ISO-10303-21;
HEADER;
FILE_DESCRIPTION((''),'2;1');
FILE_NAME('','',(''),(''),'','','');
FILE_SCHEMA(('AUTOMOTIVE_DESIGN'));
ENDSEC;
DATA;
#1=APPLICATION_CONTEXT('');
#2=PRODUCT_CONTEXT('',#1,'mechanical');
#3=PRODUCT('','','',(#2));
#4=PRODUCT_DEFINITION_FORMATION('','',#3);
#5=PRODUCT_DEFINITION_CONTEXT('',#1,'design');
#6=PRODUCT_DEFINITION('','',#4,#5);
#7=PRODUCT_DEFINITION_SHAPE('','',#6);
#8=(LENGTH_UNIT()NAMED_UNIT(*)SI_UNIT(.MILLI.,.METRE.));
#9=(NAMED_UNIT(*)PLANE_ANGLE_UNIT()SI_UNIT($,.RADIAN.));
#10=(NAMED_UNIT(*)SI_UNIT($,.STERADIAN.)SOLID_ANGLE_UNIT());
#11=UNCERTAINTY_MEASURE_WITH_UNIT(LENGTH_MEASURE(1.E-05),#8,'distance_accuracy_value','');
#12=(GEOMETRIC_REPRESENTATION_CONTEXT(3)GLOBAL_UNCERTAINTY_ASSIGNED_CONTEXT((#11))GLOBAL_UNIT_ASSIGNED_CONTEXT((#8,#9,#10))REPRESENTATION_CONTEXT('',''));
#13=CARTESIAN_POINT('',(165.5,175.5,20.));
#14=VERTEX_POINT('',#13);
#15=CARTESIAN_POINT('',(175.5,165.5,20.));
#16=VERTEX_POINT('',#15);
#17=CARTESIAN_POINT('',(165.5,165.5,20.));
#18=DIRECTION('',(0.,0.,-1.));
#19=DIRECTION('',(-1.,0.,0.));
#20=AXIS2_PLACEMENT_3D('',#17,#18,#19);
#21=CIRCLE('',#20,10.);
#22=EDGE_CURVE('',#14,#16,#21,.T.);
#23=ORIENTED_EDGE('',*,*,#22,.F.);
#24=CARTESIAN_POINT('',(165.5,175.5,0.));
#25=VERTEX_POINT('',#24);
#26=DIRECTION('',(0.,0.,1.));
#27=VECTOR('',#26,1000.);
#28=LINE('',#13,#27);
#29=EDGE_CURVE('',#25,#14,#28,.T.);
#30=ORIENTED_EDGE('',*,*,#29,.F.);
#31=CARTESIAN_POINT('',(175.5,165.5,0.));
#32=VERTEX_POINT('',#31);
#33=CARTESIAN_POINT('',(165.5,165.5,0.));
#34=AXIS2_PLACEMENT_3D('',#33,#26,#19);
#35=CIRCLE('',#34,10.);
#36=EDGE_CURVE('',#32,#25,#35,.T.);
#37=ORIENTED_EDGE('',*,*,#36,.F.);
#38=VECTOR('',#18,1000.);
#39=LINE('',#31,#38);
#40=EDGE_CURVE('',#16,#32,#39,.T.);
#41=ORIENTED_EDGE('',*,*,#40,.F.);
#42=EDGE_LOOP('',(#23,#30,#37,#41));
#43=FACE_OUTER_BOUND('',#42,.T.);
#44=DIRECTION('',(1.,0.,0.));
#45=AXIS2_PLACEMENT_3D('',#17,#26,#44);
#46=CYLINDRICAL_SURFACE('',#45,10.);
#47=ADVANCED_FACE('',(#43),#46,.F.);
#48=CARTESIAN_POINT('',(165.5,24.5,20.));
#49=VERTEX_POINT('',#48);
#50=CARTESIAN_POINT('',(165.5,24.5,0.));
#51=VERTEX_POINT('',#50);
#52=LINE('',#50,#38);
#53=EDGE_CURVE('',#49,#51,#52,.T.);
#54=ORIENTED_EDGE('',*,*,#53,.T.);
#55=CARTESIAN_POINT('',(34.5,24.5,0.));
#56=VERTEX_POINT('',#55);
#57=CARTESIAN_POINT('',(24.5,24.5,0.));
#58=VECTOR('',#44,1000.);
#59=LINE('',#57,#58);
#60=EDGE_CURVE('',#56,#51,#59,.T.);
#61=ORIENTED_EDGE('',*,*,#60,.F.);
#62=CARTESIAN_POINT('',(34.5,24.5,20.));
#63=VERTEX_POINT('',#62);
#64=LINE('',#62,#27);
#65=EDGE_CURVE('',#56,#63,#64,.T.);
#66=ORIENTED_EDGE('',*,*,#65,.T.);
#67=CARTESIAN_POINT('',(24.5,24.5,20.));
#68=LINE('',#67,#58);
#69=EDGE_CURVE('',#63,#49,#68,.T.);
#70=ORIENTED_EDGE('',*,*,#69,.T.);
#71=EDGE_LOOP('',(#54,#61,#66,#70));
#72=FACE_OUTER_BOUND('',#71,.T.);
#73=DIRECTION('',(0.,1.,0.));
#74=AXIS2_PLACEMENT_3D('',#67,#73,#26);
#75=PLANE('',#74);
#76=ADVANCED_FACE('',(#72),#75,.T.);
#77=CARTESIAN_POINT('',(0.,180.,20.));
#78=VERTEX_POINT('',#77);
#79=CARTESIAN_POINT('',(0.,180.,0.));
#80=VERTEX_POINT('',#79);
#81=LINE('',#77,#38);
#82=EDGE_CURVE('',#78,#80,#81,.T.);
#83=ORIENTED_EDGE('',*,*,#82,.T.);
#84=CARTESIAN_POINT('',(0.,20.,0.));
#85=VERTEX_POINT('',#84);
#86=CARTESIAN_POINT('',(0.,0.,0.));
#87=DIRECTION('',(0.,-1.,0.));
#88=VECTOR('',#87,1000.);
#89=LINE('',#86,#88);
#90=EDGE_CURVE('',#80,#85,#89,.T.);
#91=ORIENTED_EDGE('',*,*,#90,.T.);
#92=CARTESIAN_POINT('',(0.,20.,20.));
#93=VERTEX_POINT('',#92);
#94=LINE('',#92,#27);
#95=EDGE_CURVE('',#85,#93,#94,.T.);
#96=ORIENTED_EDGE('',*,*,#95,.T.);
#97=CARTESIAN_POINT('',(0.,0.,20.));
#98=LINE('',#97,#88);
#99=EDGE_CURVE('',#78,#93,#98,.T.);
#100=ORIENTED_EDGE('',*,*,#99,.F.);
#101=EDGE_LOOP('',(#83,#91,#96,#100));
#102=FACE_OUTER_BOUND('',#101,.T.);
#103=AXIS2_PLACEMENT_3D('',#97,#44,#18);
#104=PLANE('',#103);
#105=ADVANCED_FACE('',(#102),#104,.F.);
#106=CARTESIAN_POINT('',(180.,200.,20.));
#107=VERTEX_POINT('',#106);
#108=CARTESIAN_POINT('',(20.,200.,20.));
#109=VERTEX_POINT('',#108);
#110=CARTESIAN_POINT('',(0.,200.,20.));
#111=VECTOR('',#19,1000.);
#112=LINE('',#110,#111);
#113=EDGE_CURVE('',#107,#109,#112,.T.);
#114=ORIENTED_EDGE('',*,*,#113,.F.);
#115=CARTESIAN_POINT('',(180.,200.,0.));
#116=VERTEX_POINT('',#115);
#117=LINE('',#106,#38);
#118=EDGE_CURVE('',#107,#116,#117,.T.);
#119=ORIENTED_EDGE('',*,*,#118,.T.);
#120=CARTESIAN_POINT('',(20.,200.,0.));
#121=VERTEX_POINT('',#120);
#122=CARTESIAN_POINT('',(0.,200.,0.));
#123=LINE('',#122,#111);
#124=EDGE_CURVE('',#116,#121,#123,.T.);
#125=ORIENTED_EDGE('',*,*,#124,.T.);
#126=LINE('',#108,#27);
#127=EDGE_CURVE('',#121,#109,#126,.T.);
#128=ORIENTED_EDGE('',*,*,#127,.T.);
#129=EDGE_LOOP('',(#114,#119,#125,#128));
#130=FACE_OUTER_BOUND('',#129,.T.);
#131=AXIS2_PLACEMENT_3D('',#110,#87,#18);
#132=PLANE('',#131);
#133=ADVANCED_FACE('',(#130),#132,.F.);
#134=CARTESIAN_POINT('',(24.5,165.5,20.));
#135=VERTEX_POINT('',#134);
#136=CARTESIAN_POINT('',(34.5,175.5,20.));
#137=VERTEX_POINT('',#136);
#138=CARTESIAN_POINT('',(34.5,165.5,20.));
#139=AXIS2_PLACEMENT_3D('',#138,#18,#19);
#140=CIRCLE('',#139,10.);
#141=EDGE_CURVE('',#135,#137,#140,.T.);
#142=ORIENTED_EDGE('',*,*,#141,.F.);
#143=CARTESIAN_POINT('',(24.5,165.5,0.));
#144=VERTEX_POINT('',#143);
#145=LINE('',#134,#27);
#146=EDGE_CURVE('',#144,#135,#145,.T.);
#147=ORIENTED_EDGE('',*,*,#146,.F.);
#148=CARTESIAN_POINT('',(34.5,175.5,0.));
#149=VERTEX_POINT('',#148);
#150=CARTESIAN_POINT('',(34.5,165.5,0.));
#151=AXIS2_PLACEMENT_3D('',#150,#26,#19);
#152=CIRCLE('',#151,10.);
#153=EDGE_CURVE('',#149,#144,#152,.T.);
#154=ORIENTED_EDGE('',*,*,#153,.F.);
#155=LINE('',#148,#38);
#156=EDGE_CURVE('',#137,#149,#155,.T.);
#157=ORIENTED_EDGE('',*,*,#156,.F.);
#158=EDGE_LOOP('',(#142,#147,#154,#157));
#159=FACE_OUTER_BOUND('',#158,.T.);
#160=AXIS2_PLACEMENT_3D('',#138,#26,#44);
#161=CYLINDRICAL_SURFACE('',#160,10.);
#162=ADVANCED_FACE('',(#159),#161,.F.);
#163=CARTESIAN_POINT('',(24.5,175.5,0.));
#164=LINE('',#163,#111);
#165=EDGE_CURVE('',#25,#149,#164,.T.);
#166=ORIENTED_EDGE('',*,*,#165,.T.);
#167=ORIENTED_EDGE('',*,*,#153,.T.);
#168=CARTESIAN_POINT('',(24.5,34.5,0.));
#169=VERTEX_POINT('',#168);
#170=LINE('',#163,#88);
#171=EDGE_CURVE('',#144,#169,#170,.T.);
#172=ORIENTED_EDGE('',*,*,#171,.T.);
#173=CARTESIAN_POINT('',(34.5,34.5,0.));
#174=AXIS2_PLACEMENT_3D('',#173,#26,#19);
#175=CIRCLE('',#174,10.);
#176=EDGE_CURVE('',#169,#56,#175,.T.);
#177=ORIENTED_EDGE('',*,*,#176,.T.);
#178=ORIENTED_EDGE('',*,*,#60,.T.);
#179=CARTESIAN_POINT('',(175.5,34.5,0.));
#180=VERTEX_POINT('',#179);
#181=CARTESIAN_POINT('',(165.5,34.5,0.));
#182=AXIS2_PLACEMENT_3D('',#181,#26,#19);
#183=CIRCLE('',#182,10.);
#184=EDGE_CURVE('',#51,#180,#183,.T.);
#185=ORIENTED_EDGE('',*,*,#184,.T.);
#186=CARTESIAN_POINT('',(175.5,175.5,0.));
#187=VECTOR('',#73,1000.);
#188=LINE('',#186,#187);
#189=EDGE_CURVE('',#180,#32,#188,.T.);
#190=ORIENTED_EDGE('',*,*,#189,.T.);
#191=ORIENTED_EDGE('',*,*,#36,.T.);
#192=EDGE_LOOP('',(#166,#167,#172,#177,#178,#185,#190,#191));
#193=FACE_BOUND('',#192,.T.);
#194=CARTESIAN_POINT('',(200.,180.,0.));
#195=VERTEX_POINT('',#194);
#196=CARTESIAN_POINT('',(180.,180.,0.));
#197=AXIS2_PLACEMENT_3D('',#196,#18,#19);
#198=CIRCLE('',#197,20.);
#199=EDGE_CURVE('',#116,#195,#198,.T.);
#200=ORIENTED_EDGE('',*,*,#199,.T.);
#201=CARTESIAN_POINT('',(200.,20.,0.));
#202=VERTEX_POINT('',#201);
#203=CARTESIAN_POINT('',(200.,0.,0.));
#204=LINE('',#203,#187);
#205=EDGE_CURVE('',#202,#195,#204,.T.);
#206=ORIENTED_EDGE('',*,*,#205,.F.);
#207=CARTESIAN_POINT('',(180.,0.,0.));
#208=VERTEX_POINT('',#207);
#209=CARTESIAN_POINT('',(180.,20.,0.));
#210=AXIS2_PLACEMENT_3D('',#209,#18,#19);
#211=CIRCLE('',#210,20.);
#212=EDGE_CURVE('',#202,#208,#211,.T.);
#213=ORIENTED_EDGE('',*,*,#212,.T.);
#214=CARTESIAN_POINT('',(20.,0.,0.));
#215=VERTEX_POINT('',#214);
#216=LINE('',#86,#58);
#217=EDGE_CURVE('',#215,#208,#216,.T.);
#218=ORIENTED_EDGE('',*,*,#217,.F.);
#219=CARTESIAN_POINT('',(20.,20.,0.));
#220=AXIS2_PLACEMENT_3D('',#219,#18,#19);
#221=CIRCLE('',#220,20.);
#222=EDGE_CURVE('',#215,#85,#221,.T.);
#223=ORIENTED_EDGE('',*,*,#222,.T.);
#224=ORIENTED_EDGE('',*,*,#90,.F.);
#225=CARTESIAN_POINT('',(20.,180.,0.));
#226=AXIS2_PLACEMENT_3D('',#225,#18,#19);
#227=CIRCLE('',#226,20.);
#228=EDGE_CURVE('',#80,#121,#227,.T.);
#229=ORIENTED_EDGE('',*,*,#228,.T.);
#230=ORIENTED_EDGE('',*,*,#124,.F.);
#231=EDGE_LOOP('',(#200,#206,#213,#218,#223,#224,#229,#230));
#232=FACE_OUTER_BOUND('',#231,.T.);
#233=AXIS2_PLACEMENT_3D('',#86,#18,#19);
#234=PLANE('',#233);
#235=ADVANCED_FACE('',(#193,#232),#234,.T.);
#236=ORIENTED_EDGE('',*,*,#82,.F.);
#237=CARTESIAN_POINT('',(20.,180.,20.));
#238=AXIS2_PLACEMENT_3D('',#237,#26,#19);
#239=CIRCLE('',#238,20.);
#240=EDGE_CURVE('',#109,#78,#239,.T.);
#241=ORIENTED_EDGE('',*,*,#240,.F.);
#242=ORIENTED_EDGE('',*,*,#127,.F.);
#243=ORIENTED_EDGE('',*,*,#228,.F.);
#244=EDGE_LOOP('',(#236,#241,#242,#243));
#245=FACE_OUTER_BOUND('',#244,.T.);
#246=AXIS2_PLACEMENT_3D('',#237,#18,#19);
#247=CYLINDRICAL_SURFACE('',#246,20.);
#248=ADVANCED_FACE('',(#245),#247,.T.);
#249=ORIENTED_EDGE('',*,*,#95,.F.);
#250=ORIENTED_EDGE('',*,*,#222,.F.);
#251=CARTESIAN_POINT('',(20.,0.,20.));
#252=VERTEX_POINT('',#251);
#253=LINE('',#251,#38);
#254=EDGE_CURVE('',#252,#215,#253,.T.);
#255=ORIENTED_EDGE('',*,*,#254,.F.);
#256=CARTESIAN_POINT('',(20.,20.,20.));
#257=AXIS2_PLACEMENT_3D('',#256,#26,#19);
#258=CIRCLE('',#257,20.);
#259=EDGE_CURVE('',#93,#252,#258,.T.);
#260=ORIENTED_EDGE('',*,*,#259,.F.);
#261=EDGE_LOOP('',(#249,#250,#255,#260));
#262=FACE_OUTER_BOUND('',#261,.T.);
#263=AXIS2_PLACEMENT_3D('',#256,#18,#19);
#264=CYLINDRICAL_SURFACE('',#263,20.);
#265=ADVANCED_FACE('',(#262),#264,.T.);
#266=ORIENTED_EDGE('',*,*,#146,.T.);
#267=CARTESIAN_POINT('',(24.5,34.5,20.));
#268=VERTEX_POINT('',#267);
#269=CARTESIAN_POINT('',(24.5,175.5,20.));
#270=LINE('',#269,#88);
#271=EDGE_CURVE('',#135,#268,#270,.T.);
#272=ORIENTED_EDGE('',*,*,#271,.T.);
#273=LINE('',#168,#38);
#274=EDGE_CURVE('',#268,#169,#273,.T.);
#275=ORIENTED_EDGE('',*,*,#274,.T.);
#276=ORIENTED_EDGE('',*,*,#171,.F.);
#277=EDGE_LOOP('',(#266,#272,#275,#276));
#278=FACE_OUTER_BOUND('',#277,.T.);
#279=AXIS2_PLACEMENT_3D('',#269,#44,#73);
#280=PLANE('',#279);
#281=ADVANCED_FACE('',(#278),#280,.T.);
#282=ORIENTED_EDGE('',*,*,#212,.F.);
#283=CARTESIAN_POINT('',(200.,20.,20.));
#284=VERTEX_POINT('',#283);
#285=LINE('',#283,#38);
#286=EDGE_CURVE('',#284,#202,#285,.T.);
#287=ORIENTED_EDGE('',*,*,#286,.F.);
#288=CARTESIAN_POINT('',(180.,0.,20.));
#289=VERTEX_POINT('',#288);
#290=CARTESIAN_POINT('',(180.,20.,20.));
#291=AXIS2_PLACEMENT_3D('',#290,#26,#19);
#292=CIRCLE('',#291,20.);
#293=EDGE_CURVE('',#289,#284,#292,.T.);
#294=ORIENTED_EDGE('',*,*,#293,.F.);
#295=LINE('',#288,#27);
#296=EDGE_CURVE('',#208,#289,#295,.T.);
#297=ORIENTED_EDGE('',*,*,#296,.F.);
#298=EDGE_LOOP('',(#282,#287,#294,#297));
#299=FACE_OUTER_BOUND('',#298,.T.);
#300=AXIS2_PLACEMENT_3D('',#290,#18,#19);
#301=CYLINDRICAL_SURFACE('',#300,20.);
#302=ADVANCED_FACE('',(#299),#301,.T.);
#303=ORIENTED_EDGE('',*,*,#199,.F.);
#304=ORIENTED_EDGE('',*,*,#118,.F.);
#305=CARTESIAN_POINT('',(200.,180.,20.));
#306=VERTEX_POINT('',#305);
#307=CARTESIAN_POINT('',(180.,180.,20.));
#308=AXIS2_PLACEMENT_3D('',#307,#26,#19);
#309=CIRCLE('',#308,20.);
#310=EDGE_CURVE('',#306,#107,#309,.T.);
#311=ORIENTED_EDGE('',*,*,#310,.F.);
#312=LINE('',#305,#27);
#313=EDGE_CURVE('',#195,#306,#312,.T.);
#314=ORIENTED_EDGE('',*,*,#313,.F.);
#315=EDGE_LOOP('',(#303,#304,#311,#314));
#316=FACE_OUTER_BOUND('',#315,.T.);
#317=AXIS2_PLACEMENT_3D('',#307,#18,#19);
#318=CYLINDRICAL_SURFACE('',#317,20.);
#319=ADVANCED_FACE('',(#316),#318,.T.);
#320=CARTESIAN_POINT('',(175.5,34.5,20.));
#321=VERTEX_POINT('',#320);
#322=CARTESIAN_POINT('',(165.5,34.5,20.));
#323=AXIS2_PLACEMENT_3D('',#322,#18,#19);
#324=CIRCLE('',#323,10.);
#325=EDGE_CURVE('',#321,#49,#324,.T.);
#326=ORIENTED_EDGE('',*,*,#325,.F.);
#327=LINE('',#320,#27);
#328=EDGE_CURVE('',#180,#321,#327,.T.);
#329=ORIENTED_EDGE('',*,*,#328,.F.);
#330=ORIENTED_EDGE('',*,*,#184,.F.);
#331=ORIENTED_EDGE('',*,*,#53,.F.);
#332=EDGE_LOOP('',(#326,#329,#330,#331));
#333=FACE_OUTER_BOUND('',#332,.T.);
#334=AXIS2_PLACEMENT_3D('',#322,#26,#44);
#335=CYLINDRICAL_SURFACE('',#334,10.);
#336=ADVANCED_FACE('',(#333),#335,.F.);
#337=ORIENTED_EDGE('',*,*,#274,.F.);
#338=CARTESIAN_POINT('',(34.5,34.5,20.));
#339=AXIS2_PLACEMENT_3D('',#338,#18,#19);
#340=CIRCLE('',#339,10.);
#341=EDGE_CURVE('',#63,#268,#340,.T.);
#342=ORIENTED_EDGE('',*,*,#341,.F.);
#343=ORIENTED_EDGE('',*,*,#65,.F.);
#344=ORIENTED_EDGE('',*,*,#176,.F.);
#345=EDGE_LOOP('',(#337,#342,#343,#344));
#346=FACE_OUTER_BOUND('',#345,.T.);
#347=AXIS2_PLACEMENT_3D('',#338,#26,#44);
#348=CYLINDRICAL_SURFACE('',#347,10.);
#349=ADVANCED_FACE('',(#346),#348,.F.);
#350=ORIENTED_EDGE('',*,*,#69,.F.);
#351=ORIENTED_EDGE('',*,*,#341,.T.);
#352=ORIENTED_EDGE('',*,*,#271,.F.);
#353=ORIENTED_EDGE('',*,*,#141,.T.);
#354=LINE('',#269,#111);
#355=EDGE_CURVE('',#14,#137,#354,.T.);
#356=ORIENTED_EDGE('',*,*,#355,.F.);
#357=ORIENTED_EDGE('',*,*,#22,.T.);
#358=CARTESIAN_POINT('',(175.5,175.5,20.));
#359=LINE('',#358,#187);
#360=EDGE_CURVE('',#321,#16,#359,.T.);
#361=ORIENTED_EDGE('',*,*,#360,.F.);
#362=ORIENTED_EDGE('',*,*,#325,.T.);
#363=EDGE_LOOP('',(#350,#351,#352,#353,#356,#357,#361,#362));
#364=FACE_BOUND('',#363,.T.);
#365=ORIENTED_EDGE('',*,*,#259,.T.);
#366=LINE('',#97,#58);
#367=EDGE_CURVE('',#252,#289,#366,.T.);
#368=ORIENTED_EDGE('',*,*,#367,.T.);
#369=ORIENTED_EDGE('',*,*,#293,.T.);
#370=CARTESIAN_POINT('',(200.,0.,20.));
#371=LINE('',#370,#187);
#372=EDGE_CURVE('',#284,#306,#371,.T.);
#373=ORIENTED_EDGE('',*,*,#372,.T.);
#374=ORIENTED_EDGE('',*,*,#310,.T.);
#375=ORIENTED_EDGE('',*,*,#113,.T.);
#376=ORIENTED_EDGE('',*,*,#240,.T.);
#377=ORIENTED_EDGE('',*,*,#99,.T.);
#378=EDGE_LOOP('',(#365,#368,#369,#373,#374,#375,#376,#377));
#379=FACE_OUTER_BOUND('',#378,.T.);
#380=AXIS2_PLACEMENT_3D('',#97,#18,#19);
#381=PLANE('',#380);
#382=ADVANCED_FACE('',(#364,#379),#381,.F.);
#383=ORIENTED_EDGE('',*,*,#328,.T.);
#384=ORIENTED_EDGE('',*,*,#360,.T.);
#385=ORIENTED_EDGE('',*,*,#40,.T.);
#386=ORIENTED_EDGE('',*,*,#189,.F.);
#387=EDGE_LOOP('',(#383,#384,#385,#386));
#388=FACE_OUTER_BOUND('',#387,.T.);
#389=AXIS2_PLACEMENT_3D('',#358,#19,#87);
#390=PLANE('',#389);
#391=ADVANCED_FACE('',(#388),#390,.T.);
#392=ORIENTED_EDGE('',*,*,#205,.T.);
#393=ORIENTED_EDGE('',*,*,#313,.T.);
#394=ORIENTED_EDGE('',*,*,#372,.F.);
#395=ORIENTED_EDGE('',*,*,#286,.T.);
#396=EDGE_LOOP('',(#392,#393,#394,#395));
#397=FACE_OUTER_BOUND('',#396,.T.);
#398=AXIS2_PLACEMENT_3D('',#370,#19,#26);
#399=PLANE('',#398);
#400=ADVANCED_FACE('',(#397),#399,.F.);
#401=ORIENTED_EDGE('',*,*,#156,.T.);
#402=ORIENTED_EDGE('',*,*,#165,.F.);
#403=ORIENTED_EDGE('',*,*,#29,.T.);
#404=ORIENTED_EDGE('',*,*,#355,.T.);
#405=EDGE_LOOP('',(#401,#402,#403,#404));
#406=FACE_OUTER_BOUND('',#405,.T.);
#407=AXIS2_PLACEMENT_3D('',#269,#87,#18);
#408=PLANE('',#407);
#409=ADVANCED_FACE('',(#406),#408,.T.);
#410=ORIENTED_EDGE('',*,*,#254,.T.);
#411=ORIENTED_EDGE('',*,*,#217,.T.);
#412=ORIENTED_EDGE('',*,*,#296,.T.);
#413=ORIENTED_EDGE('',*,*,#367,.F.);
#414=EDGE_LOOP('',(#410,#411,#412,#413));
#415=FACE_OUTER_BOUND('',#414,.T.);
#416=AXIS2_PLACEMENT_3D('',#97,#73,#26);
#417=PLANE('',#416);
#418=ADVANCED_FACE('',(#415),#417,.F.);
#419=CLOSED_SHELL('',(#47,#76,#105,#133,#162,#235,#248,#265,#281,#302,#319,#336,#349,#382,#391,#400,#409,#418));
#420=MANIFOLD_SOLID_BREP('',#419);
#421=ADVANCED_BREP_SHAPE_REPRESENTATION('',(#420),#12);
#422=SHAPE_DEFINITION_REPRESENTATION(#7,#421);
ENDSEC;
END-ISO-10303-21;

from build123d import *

# Parameters (mm, degrees)
SKETCH1_W           = 200
SKETCH1_H           = 200
SKETCH1_W_2         = 151
SKETCH1_H_2         = 151
BOSS_EXTRUDE1_DEPTH = 20
FILLET1_R           = 20
FILLET2_R           = 10


with BuildPart() as part:
    # Sketch1 → Boss-Extrude1 (new body)
    with BuildSketch(Plane.XY):
        with Locations((100, 100)):
            Rectangle(SKETCH1_W, SKETCH1_H)
        with Locations((100, 100)):
            Rectangle(SKETCH1_W_2, SKETCH1_H_2, mode=Mode.SUBTRACT)
    extrude(amount=BOSS_EXTRUDE1_DEPTH)

    # Fillet1
    fillet1_edges = [part.edges().sort_by_distance(p)[0] for p in [
        (0, 200, 10),
        (200, 200, 10),
        (200, 0, 10),
        (0, 0, 10),
    ]]
    fillet(fillet1_edges, radius=FILLET1_R)

    # Fillet2
    fillet2_edges = [part.edges().sort_by_distance(p)[0] for p in [
        (24.5, 175.5, 10),
        (24.5, 24.5, 10),
        (175.5, 24.5, 10),
        (175.5, 175.5, 10),
    ]]
    fillet(fillet2_edges, radius=FILLET2_R)


solid = part.part
